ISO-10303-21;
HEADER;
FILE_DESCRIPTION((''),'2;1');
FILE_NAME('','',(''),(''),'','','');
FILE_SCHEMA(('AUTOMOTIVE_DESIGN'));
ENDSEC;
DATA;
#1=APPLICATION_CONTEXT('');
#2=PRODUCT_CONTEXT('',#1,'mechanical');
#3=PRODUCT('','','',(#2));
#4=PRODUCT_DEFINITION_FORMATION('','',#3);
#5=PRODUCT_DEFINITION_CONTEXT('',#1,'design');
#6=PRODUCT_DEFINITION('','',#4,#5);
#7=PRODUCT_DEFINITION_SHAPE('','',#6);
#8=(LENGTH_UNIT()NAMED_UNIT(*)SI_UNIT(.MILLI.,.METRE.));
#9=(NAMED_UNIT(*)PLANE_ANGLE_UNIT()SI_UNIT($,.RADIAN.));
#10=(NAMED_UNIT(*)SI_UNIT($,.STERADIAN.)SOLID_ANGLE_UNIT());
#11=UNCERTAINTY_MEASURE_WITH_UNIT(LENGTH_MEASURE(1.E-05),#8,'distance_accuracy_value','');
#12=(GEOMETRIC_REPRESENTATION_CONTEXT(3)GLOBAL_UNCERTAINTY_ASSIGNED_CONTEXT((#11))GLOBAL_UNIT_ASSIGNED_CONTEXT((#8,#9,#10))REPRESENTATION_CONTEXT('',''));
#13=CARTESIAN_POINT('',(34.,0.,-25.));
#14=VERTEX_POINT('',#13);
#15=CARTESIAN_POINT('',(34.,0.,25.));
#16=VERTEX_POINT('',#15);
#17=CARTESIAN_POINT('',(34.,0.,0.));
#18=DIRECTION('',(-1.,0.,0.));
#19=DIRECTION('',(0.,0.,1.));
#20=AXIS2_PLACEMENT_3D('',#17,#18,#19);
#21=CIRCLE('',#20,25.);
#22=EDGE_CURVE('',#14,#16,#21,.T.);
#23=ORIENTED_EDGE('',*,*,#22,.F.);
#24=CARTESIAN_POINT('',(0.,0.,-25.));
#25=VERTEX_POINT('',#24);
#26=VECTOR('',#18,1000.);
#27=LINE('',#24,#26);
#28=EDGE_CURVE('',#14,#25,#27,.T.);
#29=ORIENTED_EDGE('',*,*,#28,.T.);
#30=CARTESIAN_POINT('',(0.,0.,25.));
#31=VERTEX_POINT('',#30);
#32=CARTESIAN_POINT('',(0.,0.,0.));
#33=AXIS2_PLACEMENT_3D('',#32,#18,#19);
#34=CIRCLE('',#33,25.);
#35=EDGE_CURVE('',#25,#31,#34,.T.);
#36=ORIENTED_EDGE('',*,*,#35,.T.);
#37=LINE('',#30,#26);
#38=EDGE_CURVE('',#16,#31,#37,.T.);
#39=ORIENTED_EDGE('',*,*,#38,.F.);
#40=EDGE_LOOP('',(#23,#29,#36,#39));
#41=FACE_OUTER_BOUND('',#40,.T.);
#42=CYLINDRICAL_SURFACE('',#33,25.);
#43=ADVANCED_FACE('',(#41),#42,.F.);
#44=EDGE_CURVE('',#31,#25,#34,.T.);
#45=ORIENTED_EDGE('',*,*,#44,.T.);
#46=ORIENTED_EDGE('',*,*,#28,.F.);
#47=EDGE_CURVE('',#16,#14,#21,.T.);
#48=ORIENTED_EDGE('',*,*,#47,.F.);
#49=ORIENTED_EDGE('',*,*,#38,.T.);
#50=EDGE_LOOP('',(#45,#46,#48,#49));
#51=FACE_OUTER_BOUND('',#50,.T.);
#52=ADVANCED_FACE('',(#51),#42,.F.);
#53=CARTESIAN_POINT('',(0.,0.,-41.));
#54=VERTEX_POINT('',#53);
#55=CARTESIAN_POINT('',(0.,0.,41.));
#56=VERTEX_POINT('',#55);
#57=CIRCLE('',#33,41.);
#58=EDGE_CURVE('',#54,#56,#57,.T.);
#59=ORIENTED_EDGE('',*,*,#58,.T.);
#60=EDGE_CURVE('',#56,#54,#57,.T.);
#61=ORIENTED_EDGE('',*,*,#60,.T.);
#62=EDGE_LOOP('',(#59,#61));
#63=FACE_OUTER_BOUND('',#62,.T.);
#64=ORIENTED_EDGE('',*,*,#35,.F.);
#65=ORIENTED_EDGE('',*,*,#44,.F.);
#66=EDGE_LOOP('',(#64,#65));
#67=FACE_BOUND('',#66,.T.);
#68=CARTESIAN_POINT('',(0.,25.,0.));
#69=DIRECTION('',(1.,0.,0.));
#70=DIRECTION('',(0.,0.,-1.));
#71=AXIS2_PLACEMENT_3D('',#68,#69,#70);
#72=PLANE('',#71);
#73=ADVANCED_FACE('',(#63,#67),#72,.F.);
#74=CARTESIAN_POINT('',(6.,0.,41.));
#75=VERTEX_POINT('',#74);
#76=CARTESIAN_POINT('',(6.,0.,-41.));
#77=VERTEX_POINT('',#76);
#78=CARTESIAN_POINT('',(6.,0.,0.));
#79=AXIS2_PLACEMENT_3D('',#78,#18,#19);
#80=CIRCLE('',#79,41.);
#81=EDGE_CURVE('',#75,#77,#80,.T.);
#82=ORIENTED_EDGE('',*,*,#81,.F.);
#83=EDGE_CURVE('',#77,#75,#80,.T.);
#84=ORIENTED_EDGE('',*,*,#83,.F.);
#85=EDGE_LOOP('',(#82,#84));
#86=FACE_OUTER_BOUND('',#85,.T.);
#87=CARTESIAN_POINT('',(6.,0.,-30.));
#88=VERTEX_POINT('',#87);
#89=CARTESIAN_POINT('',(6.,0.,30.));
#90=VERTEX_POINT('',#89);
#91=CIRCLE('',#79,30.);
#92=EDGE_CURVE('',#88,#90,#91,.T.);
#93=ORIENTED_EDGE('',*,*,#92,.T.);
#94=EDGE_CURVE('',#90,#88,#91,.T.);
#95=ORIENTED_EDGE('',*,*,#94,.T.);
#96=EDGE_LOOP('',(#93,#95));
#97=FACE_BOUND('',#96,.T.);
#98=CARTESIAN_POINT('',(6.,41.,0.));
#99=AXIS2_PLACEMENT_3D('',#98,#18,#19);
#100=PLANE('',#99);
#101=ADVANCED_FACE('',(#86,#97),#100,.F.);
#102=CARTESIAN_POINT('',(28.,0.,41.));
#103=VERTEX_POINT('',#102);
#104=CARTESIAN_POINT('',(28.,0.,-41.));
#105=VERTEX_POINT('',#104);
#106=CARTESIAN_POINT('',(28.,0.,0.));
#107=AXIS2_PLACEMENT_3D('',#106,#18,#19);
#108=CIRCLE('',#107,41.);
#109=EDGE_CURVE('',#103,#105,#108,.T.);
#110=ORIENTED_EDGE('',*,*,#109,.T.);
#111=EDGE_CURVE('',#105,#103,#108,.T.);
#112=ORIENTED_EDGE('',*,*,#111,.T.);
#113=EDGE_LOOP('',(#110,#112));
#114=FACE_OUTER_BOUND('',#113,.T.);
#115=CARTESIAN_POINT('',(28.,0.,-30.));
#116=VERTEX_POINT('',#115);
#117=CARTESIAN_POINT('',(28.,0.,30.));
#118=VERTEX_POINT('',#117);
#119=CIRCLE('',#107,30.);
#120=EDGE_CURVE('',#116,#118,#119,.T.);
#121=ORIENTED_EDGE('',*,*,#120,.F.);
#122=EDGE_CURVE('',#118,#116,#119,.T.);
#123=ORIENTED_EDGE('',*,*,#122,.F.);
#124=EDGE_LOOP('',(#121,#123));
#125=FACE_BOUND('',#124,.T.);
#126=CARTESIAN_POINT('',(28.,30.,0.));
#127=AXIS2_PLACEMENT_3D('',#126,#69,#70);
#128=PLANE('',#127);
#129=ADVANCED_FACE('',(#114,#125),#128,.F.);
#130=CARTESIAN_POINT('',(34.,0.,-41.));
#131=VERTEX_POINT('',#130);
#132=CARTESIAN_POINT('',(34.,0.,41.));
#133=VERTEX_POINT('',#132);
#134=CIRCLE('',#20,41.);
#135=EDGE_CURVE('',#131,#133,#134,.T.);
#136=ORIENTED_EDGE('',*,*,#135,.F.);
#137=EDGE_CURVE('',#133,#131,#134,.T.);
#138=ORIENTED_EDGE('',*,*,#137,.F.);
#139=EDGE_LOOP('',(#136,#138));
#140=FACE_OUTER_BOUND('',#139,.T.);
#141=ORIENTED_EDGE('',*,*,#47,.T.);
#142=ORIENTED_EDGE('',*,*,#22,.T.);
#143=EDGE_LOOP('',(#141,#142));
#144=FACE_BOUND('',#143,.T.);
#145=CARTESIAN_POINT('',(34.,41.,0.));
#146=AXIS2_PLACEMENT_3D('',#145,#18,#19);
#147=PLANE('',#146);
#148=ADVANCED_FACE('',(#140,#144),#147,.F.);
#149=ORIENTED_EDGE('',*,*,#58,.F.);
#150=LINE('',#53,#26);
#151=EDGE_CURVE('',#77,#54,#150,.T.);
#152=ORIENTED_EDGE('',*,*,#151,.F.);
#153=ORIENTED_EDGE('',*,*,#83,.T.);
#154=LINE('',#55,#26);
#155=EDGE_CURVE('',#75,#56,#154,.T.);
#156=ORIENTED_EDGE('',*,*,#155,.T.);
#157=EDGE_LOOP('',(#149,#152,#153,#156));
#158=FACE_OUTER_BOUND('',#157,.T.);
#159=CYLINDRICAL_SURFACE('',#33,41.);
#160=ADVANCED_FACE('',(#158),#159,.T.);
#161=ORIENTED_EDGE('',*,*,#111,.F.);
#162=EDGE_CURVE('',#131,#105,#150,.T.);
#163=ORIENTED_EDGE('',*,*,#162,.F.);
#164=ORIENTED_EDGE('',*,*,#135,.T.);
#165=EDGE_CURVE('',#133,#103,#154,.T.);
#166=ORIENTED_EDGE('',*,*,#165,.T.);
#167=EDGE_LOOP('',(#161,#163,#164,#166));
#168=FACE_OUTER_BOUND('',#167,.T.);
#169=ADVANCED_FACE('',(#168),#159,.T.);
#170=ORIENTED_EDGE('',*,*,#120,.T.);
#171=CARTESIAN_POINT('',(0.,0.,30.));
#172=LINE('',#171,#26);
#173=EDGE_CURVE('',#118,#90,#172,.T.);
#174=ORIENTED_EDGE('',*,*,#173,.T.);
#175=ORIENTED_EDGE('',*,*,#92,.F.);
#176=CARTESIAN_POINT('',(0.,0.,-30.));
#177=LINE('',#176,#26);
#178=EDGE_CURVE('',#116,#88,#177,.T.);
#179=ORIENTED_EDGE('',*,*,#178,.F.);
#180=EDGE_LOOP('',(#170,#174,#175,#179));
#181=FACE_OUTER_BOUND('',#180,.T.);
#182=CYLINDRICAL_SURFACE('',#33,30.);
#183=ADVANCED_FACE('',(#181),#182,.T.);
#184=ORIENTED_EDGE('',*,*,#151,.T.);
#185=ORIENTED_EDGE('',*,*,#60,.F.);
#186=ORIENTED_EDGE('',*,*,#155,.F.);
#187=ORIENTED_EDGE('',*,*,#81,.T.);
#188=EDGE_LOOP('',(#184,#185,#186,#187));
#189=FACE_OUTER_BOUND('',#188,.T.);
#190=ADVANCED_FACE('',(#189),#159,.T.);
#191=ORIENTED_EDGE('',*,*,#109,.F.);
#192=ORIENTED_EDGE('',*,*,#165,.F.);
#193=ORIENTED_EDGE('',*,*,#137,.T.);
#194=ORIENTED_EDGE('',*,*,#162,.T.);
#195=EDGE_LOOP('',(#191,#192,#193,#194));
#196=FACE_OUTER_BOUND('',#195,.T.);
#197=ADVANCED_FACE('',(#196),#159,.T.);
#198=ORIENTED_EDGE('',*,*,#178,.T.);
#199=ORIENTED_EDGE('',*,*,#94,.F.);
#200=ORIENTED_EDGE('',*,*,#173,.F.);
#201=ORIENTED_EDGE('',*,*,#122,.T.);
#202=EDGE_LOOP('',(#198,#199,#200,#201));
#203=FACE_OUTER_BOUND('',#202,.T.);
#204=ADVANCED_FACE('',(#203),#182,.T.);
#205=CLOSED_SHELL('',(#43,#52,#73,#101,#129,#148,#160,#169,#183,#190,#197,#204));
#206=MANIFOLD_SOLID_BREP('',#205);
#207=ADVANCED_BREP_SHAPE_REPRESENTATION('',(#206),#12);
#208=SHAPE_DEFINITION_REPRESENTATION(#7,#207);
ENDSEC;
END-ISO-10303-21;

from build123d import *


with BuildPart() as part:
    # 草图1 → 旋转1 (revolve)
    with BuildSketch(Plane.XY, mode=Mode.PRIVATE) as revolve_1_sk:
        Polygon((0, 25), (0, 41), (6, 41), (6, 30), (28, 30), (28, 41), (34, 41), (34, 25), align=None)
    revolve(revolve_1_sk.sketch.rotate(Axis((0, 0, 0), (1, 0, 0)), 90), axis=Axis((0, 0, 0), (1, 0, 0)))


solid = part.part
